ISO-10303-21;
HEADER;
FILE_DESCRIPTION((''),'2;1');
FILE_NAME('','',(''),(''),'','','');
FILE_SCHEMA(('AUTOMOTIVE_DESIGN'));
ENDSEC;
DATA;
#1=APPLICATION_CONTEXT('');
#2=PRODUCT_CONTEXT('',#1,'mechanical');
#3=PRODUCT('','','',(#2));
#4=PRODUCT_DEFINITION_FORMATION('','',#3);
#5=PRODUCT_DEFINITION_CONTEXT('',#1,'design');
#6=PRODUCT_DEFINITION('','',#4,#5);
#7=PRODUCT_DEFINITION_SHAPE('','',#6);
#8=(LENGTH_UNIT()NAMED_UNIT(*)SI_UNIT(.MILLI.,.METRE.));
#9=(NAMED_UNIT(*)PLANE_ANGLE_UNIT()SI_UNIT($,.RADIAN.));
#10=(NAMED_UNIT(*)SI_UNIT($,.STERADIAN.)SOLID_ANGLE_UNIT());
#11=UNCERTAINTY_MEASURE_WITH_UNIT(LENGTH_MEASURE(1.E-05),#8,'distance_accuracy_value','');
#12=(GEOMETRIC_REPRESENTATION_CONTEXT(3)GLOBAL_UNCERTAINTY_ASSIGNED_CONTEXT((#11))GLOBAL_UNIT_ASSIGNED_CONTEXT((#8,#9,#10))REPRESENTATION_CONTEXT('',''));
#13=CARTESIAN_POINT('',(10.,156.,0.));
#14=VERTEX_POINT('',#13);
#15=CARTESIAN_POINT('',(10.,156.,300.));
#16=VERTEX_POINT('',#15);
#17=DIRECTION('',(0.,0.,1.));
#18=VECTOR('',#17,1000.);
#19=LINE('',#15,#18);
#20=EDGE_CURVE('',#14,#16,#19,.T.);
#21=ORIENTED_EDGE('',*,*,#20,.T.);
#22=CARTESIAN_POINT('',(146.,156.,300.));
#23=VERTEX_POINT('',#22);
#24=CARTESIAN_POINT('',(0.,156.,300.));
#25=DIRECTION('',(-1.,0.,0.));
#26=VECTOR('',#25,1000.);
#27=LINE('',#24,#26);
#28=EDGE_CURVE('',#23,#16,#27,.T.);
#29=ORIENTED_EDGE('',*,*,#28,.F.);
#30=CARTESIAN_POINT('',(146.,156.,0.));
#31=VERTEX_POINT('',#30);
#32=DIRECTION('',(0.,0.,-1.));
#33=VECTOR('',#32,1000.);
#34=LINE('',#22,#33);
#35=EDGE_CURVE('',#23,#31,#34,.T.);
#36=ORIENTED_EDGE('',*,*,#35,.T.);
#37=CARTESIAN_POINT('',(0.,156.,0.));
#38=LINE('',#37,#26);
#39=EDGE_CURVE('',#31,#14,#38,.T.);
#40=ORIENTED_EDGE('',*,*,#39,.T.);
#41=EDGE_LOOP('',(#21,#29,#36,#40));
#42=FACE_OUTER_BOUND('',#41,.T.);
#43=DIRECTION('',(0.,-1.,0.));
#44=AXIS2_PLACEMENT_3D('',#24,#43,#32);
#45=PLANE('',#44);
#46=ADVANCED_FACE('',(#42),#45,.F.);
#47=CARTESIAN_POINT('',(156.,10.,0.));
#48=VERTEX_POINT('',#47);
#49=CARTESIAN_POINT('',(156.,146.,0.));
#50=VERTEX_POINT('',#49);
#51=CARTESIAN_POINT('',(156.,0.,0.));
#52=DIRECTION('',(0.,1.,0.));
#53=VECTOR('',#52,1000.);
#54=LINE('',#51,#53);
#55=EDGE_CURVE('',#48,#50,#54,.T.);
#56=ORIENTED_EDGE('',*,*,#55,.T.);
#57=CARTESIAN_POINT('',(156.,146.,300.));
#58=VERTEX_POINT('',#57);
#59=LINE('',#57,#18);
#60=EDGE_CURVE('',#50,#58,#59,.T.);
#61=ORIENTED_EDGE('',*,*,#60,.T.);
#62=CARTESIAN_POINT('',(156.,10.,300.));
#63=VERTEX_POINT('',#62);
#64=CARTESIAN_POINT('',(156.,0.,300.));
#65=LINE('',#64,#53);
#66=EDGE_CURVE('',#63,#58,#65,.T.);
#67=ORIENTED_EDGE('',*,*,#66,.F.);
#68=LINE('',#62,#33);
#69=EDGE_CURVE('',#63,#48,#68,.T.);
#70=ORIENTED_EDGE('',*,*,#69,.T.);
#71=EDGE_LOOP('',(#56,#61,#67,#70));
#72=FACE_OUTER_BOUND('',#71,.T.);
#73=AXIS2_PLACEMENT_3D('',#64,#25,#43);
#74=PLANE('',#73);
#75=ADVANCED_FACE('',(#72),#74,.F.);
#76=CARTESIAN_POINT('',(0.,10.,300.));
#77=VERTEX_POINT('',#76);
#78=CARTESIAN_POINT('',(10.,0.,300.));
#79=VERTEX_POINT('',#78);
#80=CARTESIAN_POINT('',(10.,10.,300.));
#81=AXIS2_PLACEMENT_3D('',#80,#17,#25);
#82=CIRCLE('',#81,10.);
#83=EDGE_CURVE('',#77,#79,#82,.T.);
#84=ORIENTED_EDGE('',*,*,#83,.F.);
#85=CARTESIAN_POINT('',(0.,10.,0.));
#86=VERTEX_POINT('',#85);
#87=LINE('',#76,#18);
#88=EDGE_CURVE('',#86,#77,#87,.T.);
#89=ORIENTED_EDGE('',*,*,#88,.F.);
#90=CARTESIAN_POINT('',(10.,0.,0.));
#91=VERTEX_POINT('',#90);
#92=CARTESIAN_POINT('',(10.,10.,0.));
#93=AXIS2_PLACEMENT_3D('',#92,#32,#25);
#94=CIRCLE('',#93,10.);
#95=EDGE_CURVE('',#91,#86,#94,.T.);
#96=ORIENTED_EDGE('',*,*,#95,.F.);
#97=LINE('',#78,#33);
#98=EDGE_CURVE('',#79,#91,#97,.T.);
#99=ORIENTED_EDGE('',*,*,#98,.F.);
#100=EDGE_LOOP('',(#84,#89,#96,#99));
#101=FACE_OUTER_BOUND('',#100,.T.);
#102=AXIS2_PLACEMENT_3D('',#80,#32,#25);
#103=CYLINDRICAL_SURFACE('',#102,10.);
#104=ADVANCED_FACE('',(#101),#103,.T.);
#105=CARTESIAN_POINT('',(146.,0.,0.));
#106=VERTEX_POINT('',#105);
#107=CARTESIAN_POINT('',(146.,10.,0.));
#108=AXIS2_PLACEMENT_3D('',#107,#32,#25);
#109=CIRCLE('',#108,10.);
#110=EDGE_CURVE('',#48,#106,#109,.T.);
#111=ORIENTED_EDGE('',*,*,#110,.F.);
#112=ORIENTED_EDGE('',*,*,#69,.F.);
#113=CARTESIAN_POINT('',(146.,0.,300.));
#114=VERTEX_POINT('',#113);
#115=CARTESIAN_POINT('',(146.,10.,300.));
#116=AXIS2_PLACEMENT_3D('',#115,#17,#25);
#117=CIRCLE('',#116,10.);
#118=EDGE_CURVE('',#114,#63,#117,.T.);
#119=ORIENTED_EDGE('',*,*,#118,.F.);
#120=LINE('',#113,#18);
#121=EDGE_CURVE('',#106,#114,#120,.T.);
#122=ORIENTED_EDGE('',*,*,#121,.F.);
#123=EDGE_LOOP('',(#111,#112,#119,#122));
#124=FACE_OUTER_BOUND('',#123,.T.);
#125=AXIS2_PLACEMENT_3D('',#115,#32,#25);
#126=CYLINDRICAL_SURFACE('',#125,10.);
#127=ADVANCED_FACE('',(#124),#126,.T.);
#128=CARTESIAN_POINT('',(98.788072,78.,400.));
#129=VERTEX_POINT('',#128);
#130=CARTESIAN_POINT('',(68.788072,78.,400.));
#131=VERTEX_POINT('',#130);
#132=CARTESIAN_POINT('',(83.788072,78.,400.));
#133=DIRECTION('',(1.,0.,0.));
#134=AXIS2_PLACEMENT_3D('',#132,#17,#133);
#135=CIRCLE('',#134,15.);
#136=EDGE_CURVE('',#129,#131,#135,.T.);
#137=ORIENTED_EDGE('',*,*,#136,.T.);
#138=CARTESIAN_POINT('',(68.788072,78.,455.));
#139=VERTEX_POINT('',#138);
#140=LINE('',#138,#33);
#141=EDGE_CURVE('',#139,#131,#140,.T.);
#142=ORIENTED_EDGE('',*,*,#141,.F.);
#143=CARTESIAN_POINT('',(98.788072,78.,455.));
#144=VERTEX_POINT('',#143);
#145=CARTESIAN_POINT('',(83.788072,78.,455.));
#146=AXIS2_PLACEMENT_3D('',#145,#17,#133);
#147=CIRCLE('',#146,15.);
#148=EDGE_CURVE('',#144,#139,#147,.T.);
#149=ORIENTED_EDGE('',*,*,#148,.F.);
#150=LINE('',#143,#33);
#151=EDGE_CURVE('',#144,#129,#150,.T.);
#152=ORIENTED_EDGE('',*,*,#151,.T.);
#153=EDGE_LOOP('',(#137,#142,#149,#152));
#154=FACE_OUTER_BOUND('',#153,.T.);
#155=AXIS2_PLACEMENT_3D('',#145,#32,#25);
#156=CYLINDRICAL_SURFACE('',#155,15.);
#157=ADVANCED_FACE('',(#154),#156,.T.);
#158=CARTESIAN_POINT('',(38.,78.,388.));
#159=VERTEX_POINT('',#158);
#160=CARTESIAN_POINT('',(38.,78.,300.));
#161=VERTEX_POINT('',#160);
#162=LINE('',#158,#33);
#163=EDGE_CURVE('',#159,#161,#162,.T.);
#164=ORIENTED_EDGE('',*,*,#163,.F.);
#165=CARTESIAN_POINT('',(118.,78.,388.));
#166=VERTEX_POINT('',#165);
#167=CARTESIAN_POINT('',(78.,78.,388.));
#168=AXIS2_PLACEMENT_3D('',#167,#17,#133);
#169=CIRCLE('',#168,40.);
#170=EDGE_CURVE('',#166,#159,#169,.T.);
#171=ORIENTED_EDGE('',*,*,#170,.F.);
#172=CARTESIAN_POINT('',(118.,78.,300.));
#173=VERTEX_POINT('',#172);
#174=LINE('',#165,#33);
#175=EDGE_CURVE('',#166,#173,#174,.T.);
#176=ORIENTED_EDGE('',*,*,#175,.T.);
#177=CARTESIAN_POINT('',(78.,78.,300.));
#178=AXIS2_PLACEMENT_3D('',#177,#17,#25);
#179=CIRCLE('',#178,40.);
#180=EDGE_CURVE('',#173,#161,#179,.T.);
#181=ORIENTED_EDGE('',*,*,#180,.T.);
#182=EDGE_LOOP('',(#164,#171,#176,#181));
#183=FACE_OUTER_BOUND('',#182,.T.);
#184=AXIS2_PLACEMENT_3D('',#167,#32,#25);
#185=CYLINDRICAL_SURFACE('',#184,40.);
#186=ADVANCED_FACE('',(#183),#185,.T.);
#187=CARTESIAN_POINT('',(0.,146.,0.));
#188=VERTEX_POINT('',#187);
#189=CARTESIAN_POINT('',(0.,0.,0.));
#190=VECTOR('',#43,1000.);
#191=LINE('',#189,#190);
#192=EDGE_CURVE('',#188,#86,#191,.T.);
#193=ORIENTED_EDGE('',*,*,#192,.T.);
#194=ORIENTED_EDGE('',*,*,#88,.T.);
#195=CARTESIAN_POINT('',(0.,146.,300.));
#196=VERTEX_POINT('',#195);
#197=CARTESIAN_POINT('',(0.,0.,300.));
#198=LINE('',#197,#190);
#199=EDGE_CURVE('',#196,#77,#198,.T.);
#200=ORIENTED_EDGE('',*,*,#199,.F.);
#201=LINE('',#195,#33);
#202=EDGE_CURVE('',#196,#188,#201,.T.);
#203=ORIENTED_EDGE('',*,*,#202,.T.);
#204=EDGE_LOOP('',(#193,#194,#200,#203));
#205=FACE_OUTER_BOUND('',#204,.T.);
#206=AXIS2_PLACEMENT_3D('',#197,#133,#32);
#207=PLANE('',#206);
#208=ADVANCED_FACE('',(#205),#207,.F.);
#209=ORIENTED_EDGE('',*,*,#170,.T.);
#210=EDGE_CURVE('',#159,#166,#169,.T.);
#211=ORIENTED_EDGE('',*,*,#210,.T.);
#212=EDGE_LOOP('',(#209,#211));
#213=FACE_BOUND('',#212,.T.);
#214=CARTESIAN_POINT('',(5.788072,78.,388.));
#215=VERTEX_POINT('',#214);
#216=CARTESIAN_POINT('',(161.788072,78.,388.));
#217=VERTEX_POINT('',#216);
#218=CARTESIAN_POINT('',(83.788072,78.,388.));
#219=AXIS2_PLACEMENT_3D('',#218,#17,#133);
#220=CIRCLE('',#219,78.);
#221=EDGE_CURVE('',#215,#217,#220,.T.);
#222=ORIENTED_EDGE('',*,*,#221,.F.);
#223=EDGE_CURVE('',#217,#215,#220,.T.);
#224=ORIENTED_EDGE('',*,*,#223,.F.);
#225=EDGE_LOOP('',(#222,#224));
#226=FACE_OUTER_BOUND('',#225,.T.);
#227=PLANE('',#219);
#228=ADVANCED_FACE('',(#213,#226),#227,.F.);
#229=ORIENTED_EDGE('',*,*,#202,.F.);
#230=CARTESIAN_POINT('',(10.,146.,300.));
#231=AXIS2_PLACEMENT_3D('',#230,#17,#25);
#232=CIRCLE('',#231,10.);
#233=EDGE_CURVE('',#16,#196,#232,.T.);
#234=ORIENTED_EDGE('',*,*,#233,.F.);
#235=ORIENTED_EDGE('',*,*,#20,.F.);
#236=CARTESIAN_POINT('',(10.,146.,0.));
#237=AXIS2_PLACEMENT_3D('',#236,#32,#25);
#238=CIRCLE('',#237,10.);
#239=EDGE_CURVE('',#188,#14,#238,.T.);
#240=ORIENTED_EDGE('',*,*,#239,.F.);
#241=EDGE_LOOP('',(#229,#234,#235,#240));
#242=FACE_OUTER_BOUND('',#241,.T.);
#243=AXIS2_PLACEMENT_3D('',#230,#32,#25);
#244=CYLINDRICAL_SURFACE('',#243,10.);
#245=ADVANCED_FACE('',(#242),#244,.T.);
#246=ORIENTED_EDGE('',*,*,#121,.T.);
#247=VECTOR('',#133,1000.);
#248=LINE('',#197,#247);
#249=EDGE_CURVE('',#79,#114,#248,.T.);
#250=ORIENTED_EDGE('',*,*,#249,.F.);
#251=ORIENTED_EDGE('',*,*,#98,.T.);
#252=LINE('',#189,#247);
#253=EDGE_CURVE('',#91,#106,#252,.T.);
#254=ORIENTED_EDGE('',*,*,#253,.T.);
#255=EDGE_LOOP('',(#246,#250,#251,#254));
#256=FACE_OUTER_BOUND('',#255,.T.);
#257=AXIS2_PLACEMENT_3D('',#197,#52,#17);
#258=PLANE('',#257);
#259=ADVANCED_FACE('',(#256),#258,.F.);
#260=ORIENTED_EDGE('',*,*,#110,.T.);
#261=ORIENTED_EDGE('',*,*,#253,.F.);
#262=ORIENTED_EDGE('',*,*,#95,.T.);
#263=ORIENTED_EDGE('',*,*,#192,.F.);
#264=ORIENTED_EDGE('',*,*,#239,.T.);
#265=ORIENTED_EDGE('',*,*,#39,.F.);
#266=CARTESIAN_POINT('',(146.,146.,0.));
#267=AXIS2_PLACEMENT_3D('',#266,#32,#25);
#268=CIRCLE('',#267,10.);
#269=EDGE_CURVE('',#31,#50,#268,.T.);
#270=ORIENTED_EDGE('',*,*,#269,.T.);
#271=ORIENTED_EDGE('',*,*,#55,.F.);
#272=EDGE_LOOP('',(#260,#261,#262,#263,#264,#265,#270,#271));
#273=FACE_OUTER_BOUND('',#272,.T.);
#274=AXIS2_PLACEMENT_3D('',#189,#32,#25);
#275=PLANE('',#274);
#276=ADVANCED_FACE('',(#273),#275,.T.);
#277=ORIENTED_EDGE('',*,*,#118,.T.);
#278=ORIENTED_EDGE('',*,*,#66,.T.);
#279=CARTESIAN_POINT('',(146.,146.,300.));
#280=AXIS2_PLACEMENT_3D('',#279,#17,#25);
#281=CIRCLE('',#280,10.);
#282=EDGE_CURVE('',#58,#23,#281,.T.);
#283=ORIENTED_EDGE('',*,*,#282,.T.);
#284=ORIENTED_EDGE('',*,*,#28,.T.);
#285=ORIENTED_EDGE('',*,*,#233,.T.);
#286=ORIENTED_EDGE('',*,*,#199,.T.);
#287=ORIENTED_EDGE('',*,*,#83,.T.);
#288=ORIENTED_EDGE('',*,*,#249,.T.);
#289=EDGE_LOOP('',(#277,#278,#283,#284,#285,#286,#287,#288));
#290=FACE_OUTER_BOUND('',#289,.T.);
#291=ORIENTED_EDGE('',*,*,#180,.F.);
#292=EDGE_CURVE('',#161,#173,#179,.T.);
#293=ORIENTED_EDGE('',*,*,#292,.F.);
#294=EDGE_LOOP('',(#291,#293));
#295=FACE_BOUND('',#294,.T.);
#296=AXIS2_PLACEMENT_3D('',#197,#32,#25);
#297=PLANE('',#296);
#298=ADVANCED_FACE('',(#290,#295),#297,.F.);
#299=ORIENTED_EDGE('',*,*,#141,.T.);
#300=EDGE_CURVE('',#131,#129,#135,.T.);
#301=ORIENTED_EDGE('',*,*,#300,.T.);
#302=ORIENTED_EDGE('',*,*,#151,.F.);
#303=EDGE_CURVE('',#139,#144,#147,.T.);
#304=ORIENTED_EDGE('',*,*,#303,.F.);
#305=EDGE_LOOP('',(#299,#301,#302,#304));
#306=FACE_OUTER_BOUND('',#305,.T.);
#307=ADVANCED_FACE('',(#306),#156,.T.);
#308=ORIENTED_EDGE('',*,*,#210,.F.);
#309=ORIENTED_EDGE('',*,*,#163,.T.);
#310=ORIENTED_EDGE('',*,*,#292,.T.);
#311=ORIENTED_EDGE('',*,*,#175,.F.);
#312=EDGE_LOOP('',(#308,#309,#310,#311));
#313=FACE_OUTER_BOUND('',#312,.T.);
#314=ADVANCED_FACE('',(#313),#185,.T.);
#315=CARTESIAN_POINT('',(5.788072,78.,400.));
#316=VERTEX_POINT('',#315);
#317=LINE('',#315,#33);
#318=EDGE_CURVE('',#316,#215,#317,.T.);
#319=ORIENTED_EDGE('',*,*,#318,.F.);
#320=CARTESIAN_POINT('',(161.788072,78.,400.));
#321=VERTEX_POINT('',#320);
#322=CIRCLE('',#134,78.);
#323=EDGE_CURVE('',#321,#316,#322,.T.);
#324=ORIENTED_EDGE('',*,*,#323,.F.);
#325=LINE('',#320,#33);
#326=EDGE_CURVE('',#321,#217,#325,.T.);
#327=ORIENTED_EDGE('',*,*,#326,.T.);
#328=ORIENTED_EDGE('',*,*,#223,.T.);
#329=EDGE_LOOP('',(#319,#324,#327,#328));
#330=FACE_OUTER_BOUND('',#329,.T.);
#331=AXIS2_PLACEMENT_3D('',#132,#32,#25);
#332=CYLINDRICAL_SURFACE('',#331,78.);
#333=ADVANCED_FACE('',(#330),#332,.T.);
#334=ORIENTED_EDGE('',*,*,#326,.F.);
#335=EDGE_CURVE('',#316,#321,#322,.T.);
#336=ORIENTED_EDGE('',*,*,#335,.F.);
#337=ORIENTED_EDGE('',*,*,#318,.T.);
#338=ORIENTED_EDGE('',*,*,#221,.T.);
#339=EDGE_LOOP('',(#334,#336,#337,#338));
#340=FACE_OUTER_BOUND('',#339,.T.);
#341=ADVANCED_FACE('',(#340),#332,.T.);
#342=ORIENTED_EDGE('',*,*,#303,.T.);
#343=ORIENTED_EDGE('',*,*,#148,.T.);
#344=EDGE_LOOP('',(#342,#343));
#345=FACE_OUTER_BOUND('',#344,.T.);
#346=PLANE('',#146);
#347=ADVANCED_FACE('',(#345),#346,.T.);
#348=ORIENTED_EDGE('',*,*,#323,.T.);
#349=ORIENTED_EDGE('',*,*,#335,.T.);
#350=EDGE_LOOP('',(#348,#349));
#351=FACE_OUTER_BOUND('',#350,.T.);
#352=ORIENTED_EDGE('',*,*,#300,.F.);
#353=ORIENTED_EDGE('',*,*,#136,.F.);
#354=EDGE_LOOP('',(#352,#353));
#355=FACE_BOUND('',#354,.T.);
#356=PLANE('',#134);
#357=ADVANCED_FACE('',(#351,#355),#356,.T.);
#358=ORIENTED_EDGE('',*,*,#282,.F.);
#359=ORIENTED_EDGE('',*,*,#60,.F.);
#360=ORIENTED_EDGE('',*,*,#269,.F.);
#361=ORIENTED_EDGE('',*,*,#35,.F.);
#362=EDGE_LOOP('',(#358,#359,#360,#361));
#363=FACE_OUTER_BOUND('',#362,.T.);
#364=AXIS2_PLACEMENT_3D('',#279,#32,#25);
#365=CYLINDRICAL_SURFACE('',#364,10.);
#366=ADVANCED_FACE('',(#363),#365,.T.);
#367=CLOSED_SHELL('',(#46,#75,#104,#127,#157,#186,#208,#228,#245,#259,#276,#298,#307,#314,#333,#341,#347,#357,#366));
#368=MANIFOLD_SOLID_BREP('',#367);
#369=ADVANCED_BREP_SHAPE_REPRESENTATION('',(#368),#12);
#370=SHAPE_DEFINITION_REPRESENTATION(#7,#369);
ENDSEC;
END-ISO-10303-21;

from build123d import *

# Parameters (mm, degrees)
SKETCH1_W           = 156
SKETCH1_H           = 156
BOSS_EXTRUDE1_DEPTH = 300
SKETCH2_R           = 40
BOSS_EXTRUDE2_DEPTH = 88
SKETCH3_R           = 78
BOSS_EXTRUDE3_DEPTH = 12
FILLET1_R           = 10
SKETCH4_R           = 15
BOSS_EXTRUDE4_DEPTH = 55


with BuildPart() as part:
    # Sketch1 → Boss-Extrude1 (new body)
    with BuildSketch(Plane.XY):
        with Locations((78, 78)):
            Rectangle(SKETCH1_W, SKETCH1_H)
    extrude(amount=BOSS_EXTRUDE1_DEPTH)

    # Sketch2 → Boss-Extrude2 (add)
    with BuildSketch(Plane.XY.offset(300)):
        with Locations(Location((78, 78, 0), (0, 0, 180))):
            Circle(SKETCH2_R)
    extrude(amount=BOSS_EXTRUDE2_DEPTH)

    # Sketch3 → Boss-Extrude3 (add)
    with BuildSketch(Plane.XY.offset(388)):
        with Locations((83.788071994, 78)):
            Circle(SKETCH3_R)
    extrude(amount=BOSS_EXTRUDE3_DEPTH)

    # Fillet1
    fillet1_edges = [part.edges().sort_by_distance(p)[0] for p in [
        (0, 156, 150),
        (156, 156, 150),
        (156, 0, 150),
        (0, 0, 150),
    ]]
    fillet(fillet1_edges, radius=FILLET1_R)

    # Sketch4 → Boss-Extrude4 (add)
    with BuildSketch(Plane.XY.offset(400)):
        with Locations((83.788071994, 78)):
            Circle(SKETCH4_R)
    extrude(amount=BOSS_EXTRUDE4_DEPTH)


solid = part.part
